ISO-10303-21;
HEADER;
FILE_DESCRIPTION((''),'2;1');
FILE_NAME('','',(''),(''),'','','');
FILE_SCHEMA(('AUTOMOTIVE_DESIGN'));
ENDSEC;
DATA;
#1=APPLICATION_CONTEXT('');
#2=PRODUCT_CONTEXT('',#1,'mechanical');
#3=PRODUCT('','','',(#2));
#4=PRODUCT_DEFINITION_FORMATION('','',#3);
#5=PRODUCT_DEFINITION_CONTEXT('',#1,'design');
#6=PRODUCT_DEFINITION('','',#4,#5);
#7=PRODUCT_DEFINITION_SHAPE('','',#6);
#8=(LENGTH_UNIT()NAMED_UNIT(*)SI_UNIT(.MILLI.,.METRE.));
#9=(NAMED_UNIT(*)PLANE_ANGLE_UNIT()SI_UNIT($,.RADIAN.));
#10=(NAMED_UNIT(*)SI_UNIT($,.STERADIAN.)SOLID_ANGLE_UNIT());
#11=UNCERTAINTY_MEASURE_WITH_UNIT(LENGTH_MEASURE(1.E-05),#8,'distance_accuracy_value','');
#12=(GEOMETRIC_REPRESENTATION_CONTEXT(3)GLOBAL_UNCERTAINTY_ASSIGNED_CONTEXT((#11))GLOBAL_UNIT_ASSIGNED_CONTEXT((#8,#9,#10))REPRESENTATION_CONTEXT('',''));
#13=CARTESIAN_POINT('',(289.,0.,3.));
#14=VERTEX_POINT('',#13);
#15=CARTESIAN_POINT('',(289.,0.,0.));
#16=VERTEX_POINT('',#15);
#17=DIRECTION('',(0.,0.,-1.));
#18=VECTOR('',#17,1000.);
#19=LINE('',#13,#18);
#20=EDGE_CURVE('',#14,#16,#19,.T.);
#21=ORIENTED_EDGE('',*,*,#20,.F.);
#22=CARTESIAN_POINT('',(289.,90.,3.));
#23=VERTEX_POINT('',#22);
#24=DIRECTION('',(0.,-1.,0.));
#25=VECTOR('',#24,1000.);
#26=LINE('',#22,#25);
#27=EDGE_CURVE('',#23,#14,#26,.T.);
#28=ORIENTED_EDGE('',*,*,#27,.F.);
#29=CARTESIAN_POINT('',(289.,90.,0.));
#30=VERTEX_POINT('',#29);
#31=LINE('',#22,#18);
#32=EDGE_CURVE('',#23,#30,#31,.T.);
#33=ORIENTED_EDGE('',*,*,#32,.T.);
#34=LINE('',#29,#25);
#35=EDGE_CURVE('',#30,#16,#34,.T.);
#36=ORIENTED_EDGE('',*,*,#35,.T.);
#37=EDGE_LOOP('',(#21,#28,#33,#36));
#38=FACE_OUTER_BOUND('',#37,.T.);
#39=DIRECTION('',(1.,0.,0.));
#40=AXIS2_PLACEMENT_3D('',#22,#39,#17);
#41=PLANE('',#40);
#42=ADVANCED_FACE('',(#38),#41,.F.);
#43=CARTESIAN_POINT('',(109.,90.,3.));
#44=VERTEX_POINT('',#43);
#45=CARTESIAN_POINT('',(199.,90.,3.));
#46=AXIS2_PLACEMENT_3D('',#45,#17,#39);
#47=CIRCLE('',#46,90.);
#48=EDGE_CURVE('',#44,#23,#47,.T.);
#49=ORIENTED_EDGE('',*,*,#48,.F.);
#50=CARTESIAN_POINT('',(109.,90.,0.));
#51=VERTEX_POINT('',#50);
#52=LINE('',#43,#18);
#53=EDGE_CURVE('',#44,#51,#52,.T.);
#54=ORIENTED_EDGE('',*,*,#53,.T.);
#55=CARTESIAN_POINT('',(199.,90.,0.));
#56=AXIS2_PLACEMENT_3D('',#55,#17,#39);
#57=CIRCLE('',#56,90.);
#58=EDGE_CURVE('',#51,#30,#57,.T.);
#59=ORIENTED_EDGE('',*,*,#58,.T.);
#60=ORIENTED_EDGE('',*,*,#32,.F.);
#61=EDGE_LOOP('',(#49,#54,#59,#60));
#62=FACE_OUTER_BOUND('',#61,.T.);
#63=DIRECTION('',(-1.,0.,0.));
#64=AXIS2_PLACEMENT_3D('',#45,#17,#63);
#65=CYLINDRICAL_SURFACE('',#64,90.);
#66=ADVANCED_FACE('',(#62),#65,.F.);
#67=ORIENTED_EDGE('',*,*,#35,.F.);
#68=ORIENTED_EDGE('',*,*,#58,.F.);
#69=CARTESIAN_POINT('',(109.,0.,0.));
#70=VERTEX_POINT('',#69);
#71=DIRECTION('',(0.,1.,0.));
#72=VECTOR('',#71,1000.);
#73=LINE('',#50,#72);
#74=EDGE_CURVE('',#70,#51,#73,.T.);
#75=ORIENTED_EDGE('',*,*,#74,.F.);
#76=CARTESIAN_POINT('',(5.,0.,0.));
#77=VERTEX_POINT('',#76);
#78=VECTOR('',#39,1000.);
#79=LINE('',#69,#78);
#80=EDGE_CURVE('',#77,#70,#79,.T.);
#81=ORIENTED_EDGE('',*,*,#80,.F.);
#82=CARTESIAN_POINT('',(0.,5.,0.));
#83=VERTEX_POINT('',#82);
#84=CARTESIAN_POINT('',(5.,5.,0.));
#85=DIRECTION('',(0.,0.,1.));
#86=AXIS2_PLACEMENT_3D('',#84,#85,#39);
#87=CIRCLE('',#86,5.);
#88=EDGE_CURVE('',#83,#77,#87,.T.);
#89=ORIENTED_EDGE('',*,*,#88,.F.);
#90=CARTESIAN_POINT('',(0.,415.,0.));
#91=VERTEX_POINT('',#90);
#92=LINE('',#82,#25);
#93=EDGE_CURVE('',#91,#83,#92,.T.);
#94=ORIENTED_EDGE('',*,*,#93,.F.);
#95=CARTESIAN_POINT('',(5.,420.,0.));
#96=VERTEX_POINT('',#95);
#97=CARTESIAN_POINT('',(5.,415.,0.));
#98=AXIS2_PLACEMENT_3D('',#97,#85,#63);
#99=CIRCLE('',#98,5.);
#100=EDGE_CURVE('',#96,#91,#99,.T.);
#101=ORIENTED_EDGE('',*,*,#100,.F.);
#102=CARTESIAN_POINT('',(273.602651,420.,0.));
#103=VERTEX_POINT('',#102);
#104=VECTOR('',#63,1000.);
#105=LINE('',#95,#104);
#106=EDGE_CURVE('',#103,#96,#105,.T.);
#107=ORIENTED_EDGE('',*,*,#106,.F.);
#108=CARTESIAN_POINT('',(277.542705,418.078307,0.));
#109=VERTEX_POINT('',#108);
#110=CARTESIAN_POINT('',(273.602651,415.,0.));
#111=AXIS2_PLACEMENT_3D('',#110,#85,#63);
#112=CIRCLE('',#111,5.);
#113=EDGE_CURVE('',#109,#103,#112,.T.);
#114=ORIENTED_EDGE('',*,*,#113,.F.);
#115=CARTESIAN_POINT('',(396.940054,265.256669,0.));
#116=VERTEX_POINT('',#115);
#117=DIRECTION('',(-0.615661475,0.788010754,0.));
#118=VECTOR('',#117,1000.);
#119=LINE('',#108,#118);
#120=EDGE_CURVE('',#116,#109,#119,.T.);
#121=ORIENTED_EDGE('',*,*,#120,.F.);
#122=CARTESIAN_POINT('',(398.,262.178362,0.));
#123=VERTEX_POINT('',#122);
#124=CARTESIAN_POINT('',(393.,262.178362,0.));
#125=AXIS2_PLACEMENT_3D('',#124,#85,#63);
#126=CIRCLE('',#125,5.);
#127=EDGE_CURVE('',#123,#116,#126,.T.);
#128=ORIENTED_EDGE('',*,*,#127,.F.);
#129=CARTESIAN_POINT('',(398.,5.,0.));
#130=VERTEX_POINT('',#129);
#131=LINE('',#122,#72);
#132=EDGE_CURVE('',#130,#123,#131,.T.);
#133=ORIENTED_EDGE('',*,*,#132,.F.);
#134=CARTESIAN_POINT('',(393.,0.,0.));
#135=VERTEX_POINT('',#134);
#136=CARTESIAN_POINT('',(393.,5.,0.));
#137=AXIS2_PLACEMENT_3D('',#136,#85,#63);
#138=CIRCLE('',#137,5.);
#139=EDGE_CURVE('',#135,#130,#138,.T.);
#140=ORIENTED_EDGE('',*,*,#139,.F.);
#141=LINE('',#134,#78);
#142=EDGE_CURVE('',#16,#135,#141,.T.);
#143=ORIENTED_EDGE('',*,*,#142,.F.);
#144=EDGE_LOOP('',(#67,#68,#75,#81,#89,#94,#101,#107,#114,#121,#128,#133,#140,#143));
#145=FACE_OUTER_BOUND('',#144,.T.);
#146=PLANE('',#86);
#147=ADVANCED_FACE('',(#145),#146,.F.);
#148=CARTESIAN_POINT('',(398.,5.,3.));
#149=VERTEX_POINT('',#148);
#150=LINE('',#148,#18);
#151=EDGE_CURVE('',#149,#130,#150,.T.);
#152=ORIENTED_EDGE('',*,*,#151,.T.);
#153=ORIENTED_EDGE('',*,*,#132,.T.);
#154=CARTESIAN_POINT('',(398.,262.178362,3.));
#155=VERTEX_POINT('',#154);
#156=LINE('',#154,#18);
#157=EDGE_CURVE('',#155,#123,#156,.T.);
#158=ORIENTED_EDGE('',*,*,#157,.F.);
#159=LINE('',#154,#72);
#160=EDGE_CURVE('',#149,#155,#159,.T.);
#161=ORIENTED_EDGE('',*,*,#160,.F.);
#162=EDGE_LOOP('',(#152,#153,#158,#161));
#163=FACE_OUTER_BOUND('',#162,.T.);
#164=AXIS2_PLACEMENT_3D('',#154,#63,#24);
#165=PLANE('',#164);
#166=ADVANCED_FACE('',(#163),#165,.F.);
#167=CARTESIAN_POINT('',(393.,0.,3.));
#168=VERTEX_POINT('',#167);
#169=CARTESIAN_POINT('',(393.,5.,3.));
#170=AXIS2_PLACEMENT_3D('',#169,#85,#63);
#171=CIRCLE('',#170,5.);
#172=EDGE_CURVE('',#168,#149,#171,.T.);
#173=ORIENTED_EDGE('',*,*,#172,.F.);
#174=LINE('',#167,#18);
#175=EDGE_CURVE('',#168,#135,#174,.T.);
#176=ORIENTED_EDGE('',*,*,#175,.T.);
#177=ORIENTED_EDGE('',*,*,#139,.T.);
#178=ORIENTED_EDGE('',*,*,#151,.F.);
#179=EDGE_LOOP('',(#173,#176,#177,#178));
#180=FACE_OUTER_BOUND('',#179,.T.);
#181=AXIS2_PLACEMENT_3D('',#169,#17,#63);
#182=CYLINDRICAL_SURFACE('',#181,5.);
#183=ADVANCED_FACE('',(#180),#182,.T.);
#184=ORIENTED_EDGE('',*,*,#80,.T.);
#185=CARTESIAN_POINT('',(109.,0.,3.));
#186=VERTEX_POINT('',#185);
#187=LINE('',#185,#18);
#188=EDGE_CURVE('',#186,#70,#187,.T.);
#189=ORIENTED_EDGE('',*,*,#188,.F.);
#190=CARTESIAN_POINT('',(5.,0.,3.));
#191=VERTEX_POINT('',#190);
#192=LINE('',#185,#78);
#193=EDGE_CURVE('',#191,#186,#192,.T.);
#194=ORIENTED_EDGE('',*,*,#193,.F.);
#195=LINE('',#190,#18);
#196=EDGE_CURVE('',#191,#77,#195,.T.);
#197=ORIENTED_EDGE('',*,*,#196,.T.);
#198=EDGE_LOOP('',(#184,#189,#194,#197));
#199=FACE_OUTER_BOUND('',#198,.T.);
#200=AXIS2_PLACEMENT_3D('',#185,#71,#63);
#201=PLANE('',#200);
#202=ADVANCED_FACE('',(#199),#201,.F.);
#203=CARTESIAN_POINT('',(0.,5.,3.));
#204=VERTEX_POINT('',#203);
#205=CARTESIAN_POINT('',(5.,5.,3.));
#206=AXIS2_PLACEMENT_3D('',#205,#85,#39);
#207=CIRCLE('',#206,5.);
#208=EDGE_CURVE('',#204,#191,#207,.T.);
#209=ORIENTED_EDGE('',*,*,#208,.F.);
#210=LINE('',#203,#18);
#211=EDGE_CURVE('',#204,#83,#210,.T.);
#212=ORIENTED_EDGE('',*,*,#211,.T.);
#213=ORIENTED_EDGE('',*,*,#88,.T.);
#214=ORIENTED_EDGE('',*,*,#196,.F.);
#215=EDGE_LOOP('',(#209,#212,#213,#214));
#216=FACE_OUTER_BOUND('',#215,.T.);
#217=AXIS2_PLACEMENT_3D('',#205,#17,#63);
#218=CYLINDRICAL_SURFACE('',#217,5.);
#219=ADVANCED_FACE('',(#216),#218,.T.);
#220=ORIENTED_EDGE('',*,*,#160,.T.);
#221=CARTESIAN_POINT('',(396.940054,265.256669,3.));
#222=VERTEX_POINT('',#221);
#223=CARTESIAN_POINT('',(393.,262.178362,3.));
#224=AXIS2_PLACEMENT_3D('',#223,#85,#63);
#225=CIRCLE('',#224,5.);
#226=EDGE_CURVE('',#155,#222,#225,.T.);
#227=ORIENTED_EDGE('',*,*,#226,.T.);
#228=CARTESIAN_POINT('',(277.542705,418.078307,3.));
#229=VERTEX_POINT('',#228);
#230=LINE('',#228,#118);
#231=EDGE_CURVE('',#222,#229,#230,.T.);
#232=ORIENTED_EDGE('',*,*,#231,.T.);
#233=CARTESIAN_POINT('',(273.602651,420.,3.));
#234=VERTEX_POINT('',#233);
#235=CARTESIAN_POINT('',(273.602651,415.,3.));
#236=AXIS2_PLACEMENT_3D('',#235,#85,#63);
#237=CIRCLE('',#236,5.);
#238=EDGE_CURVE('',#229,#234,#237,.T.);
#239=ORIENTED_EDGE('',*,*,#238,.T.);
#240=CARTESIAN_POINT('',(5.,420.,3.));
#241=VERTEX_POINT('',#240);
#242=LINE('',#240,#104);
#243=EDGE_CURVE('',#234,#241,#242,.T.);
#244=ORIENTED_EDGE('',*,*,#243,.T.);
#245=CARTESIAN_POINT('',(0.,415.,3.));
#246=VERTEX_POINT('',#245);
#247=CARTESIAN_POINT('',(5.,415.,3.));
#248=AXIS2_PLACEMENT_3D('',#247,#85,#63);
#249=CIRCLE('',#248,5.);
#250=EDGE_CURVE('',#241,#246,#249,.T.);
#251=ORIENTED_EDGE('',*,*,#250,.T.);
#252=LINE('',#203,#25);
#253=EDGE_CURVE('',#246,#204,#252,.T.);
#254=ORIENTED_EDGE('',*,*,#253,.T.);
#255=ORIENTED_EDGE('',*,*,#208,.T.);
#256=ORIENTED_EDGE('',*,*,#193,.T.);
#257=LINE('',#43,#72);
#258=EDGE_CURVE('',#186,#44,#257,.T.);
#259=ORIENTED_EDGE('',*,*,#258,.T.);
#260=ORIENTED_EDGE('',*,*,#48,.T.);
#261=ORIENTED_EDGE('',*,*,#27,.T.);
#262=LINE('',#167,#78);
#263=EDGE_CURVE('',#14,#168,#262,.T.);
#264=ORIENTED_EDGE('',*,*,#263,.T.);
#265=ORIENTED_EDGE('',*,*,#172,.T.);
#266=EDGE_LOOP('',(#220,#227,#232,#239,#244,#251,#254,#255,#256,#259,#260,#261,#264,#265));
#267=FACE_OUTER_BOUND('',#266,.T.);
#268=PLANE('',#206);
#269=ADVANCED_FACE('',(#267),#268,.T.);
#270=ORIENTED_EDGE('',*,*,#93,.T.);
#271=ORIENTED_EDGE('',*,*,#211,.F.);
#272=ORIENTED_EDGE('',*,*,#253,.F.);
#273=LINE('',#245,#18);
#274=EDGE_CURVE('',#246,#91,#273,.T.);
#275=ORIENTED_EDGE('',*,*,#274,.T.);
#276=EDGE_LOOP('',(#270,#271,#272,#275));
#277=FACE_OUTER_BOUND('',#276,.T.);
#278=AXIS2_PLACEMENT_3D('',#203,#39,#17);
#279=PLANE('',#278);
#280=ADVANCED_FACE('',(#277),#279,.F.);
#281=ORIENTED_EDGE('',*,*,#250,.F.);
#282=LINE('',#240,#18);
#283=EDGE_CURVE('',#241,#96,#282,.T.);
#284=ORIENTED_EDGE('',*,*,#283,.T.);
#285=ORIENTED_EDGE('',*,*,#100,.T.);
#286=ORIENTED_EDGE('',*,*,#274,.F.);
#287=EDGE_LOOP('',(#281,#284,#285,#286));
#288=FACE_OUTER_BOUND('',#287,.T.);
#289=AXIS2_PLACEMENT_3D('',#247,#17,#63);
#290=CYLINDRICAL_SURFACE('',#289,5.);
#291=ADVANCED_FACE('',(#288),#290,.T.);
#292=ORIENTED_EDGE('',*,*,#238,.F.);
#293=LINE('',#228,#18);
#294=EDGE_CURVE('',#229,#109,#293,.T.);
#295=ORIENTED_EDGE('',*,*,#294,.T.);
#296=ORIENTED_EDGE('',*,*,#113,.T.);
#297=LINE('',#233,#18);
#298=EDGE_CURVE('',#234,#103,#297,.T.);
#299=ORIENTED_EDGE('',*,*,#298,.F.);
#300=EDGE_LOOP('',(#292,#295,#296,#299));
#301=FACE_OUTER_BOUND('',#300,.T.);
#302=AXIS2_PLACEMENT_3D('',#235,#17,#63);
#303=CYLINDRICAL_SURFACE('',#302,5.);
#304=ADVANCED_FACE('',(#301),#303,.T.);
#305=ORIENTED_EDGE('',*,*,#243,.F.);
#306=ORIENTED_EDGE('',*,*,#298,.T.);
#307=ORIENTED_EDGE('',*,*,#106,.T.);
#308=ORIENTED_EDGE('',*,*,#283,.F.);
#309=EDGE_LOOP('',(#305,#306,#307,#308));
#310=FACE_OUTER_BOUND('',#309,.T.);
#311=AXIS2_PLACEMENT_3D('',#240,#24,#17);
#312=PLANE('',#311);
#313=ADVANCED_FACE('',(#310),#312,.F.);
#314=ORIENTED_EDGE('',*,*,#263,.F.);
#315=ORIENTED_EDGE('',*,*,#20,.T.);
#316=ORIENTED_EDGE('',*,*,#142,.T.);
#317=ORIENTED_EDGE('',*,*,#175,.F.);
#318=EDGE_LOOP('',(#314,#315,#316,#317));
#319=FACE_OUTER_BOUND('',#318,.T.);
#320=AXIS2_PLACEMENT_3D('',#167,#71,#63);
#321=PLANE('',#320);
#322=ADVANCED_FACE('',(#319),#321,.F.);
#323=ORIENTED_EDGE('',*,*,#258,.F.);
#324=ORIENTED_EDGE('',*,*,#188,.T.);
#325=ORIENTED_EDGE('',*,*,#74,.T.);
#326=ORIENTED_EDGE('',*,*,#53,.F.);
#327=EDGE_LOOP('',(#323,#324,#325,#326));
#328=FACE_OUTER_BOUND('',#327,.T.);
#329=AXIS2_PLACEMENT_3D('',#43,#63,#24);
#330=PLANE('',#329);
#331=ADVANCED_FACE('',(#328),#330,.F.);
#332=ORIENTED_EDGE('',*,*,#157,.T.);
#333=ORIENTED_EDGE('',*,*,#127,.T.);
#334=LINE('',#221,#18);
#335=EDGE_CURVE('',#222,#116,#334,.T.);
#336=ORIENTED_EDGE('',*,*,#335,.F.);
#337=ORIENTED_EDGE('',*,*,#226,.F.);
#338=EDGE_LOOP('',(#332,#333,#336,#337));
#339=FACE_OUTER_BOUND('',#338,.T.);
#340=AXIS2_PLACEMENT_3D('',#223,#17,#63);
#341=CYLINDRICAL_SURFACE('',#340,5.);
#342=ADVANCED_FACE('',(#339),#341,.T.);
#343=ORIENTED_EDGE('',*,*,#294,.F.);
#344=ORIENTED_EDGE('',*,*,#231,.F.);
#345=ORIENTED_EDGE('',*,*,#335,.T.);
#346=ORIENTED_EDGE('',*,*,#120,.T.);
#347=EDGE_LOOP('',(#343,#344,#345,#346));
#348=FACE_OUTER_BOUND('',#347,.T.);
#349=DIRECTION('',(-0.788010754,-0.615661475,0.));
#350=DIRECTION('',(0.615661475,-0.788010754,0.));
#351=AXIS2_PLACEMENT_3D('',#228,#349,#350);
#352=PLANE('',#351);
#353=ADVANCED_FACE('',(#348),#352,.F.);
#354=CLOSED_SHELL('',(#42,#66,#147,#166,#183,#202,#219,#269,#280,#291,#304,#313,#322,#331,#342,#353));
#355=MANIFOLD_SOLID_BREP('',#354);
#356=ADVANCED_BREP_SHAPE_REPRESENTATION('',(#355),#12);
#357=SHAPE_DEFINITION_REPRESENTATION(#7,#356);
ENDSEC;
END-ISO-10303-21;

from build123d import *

# Parameters (mm, degrees)
BOSS_EXTRUDE1_DEPTH = 3


with BuildPart() as part:
    # Sketch1 → Boss-Extrude1 (new body)
    with BuildSketch(Plane.XY):
        with BuildLine():
            Line((0, 5), (0, 415))
            ThreePointArc((0, 415), (1.464466094, 418.535533906), (5, 420))
            Line((5, 420), (273.602650759, 420))
            ThreePointArc((273.602650759, 420), (275.794506493, 419.493970231), (277.542704528, 418.078307377))
            Line((277.542704528, 418.078307377), (396.940053768, 265.25666931))
            ThreePointArc((396.940053768, 265.25666931), (397.727592878, 263.806202706), (398, 262.178361934))
            Line((398, 262.178361934), (398, 5))
            ThreePointArc((398, 5), (396.535533906, 1.464466094), (393, 0))
            Line((393, 0), (289, 0))
            Line((289, 0), (289, 90))
            ThreePointArc((289, 90), (199, 180), (109, 90))
            Line((109, 90), (109, 0))
            Line((109, 0), (5, 0))
            ThreePointArc((5, 0), (1.464466094, 1.464466094), (0, 5))
        make_face()
    extrude(amount=BOSS_EXTRUDE1_DEPTH)


solid = part.part
